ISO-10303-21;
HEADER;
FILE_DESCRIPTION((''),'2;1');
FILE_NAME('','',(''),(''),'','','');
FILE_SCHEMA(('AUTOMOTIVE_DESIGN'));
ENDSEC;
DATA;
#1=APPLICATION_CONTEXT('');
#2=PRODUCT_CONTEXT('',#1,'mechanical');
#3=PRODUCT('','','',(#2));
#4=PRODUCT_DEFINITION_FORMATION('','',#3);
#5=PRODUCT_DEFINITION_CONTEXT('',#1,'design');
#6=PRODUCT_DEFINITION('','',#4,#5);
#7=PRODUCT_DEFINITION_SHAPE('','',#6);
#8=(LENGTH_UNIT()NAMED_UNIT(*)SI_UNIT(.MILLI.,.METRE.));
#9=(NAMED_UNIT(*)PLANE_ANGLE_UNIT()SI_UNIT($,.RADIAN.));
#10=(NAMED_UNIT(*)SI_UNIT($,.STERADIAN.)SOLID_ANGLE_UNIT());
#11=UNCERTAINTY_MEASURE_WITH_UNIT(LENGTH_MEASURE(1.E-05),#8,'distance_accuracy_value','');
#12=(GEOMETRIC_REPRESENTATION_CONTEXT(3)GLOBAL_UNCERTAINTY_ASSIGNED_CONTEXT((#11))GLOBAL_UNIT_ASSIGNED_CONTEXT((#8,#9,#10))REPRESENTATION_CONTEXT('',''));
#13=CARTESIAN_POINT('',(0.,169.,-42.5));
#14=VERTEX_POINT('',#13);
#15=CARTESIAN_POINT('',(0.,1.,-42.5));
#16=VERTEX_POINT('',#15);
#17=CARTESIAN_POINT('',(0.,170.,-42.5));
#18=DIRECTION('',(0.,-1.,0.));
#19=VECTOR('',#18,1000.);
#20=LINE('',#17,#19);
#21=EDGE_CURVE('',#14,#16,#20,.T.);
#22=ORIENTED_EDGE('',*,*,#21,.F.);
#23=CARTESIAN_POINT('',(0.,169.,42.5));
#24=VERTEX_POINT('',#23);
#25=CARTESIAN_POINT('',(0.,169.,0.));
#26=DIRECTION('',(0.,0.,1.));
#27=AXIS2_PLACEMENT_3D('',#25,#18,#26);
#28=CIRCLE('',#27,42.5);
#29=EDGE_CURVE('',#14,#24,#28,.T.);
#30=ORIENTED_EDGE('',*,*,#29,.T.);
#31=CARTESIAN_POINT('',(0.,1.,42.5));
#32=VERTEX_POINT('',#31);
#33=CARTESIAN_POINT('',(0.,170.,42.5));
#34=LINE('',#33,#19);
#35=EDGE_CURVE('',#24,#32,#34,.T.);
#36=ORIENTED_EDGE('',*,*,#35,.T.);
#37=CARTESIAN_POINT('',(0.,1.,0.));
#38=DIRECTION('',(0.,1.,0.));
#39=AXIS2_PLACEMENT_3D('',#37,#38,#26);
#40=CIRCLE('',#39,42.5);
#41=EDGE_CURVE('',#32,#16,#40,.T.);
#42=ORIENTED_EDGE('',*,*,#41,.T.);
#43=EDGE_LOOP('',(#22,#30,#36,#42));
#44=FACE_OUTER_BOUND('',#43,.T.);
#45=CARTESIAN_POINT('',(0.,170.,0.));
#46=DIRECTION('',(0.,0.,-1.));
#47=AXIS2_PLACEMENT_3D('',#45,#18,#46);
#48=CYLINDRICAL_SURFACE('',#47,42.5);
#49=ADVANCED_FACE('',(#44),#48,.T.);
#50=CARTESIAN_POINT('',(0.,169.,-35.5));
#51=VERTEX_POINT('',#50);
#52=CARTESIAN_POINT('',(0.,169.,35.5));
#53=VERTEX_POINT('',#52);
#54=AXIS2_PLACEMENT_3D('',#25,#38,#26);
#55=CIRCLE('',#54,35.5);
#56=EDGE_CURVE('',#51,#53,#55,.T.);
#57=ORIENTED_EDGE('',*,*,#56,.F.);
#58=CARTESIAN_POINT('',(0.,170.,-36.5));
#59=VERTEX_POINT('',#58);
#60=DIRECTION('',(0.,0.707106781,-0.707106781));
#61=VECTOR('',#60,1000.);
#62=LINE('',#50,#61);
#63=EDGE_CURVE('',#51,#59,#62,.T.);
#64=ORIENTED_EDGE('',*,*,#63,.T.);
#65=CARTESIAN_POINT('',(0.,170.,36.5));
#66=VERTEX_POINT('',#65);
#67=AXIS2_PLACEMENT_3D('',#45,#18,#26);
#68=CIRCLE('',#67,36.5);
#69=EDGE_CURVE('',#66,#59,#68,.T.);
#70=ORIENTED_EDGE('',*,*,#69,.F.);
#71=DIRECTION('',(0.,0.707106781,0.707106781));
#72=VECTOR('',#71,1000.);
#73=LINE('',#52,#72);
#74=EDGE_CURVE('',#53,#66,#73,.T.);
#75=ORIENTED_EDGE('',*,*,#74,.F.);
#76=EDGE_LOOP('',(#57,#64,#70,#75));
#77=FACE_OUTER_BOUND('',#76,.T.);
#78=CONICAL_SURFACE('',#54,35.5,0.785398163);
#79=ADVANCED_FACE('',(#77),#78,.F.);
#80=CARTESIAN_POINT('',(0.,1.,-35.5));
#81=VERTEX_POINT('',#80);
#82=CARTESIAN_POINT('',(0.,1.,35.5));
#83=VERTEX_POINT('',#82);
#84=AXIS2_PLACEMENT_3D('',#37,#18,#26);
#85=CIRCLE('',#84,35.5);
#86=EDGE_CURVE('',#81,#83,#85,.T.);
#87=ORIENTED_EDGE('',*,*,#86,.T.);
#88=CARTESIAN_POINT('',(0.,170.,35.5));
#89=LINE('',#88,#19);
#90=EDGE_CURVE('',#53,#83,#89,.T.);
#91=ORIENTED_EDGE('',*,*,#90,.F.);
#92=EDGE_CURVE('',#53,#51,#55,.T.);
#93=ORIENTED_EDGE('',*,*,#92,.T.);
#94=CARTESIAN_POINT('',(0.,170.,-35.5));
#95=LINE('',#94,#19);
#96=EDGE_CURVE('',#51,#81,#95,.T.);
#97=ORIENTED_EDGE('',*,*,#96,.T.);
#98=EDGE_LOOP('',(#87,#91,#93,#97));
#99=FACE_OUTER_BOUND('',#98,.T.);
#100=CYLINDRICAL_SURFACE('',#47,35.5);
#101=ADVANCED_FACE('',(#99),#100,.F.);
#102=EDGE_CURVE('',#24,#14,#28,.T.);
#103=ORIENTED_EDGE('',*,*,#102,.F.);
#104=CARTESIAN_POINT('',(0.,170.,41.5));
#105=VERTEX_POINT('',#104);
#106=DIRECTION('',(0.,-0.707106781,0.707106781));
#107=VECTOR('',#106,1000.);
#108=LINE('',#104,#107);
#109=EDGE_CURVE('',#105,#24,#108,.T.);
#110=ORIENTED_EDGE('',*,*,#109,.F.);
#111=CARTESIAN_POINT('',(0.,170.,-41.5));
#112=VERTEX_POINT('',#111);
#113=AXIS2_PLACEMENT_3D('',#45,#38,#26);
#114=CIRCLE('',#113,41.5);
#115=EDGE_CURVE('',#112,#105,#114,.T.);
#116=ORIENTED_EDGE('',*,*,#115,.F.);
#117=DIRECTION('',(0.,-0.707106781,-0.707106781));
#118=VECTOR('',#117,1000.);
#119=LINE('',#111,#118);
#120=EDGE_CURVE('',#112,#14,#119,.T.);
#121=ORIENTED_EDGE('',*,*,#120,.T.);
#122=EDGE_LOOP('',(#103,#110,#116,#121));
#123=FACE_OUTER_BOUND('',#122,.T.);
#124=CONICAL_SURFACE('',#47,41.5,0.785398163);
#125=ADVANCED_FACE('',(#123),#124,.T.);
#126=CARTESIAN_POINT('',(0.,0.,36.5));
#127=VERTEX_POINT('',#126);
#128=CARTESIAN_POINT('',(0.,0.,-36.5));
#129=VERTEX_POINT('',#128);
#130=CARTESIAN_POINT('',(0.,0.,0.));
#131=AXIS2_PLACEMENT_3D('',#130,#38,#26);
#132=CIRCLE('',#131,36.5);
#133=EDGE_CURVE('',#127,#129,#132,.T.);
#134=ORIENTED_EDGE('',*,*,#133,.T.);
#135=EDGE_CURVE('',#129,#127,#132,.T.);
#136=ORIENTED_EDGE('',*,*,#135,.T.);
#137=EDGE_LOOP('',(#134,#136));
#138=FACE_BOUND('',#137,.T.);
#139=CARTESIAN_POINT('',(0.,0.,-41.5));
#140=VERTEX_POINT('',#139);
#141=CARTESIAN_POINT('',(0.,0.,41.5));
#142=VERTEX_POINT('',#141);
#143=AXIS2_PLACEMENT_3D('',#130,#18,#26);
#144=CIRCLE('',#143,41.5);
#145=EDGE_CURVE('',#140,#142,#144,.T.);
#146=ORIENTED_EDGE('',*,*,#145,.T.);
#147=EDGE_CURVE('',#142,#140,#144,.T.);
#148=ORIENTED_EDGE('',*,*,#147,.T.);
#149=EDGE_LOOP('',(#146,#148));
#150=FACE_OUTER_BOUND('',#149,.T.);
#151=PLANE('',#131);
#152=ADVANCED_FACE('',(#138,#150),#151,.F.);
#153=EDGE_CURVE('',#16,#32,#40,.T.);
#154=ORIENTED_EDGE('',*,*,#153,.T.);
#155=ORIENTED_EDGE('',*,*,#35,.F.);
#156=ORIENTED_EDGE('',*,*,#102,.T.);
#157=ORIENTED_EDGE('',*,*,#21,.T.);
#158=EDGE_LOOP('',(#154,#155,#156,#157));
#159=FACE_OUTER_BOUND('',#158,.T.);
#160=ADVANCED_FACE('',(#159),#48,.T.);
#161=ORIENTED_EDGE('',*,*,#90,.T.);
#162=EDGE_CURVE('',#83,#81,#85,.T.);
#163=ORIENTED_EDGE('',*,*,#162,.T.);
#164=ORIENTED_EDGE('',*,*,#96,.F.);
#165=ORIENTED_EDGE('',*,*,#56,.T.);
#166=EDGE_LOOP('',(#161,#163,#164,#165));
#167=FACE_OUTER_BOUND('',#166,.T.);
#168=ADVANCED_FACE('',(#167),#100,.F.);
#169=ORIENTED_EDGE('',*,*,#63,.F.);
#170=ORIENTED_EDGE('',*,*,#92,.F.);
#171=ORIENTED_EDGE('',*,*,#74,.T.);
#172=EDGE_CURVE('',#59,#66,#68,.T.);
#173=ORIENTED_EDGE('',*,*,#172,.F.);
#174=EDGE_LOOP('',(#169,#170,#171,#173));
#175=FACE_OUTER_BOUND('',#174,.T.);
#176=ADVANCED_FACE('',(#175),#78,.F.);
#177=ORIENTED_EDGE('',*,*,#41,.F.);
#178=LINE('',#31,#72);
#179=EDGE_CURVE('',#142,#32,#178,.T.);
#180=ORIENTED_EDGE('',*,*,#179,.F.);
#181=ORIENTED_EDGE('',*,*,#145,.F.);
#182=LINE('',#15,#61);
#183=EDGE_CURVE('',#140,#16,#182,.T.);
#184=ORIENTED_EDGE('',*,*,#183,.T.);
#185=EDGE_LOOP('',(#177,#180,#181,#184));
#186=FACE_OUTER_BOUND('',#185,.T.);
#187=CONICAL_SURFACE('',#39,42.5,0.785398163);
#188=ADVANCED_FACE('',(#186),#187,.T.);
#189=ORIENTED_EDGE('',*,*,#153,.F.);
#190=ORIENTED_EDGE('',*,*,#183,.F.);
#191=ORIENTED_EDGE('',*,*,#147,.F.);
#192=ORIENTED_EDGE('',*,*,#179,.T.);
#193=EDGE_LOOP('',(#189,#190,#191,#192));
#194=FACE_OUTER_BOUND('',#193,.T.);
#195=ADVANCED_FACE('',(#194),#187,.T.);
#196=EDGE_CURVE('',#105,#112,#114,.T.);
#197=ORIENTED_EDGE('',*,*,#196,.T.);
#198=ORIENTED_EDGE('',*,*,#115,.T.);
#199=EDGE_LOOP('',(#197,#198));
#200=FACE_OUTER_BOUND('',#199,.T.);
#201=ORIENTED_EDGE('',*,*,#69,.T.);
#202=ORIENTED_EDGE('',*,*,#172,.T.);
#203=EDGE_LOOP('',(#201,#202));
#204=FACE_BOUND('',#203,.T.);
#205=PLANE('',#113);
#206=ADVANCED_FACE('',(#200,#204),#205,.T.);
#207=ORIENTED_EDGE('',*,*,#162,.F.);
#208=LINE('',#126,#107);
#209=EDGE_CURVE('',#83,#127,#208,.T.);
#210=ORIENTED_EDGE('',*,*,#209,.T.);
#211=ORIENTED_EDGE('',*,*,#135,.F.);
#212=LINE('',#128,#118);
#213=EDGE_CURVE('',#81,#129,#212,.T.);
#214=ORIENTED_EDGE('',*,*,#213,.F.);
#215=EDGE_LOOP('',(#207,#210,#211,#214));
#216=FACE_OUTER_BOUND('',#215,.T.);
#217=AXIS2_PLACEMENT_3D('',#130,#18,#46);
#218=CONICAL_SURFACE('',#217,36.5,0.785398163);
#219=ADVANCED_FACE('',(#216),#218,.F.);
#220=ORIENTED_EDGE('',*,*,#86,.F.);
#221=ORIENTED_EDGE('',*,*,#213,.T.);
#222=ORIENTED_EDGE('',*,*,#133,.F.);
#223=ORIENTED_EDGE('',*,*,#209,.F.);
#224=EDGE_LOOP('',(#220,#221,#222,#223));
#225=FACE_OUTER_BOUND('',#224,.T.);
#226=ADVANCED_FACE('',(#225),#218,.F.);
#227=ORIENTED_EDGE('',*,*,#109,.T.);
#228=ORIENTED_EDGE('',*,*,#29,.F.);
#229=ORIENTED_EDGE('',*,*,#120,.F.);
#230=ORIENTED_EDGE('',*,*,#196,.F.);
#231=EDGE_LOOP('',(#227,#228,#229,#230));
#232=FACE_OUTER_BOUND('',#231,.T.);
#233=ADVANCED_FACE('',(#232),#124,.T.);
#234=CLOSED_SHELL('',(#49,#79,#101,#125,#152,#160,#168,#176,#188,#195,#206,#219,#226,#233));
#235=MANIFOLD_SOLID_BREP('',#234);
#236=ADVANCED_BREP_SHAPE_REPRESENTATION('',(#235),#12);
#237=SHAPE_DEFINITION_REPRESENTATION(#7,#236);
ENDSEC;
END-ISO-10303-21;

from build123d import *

# Parameters (mm, degrees)
SKETCH1_R           = 42.5
SKETCH1_R_2         = 35.5
BOSS_EXTRUDE1_DEPTH = 170
CHAMFER2_SIZE       = 1


with BuildPart() as part:
    # Sketch1 → Boss-Extrude1 (new body)
    with BuildSketch(Plane(origin=(0, 0, 0), x_dir=(1, 0, 0), z_dir=(0, 1, 0))):
        with Locations(Location((0, 0, 0), (0, 0, 270))):
            Circle(SKETCH1_R)
        with Locations(Location((0, 0, 0), (0, 0, 270))):
            Circle(SKETCH1_R_2, mode=Mode.SUBTRACT)
    extrude(amount=BOSS_EXTRUDE1_DEPTH)

    # Chamfer2
    chamfer2_edges = [part.edges().sort_by_distance(p)[0] for p in [
        (0, 0, -42.5),
        (0, 170, -42.5),
        (0, 0, -35.5),
        (0, 170, -35.5),
    ]]
    chamfer(chamfer2_edges, length=CHAMFER2_SIZE)


solid = part.part
